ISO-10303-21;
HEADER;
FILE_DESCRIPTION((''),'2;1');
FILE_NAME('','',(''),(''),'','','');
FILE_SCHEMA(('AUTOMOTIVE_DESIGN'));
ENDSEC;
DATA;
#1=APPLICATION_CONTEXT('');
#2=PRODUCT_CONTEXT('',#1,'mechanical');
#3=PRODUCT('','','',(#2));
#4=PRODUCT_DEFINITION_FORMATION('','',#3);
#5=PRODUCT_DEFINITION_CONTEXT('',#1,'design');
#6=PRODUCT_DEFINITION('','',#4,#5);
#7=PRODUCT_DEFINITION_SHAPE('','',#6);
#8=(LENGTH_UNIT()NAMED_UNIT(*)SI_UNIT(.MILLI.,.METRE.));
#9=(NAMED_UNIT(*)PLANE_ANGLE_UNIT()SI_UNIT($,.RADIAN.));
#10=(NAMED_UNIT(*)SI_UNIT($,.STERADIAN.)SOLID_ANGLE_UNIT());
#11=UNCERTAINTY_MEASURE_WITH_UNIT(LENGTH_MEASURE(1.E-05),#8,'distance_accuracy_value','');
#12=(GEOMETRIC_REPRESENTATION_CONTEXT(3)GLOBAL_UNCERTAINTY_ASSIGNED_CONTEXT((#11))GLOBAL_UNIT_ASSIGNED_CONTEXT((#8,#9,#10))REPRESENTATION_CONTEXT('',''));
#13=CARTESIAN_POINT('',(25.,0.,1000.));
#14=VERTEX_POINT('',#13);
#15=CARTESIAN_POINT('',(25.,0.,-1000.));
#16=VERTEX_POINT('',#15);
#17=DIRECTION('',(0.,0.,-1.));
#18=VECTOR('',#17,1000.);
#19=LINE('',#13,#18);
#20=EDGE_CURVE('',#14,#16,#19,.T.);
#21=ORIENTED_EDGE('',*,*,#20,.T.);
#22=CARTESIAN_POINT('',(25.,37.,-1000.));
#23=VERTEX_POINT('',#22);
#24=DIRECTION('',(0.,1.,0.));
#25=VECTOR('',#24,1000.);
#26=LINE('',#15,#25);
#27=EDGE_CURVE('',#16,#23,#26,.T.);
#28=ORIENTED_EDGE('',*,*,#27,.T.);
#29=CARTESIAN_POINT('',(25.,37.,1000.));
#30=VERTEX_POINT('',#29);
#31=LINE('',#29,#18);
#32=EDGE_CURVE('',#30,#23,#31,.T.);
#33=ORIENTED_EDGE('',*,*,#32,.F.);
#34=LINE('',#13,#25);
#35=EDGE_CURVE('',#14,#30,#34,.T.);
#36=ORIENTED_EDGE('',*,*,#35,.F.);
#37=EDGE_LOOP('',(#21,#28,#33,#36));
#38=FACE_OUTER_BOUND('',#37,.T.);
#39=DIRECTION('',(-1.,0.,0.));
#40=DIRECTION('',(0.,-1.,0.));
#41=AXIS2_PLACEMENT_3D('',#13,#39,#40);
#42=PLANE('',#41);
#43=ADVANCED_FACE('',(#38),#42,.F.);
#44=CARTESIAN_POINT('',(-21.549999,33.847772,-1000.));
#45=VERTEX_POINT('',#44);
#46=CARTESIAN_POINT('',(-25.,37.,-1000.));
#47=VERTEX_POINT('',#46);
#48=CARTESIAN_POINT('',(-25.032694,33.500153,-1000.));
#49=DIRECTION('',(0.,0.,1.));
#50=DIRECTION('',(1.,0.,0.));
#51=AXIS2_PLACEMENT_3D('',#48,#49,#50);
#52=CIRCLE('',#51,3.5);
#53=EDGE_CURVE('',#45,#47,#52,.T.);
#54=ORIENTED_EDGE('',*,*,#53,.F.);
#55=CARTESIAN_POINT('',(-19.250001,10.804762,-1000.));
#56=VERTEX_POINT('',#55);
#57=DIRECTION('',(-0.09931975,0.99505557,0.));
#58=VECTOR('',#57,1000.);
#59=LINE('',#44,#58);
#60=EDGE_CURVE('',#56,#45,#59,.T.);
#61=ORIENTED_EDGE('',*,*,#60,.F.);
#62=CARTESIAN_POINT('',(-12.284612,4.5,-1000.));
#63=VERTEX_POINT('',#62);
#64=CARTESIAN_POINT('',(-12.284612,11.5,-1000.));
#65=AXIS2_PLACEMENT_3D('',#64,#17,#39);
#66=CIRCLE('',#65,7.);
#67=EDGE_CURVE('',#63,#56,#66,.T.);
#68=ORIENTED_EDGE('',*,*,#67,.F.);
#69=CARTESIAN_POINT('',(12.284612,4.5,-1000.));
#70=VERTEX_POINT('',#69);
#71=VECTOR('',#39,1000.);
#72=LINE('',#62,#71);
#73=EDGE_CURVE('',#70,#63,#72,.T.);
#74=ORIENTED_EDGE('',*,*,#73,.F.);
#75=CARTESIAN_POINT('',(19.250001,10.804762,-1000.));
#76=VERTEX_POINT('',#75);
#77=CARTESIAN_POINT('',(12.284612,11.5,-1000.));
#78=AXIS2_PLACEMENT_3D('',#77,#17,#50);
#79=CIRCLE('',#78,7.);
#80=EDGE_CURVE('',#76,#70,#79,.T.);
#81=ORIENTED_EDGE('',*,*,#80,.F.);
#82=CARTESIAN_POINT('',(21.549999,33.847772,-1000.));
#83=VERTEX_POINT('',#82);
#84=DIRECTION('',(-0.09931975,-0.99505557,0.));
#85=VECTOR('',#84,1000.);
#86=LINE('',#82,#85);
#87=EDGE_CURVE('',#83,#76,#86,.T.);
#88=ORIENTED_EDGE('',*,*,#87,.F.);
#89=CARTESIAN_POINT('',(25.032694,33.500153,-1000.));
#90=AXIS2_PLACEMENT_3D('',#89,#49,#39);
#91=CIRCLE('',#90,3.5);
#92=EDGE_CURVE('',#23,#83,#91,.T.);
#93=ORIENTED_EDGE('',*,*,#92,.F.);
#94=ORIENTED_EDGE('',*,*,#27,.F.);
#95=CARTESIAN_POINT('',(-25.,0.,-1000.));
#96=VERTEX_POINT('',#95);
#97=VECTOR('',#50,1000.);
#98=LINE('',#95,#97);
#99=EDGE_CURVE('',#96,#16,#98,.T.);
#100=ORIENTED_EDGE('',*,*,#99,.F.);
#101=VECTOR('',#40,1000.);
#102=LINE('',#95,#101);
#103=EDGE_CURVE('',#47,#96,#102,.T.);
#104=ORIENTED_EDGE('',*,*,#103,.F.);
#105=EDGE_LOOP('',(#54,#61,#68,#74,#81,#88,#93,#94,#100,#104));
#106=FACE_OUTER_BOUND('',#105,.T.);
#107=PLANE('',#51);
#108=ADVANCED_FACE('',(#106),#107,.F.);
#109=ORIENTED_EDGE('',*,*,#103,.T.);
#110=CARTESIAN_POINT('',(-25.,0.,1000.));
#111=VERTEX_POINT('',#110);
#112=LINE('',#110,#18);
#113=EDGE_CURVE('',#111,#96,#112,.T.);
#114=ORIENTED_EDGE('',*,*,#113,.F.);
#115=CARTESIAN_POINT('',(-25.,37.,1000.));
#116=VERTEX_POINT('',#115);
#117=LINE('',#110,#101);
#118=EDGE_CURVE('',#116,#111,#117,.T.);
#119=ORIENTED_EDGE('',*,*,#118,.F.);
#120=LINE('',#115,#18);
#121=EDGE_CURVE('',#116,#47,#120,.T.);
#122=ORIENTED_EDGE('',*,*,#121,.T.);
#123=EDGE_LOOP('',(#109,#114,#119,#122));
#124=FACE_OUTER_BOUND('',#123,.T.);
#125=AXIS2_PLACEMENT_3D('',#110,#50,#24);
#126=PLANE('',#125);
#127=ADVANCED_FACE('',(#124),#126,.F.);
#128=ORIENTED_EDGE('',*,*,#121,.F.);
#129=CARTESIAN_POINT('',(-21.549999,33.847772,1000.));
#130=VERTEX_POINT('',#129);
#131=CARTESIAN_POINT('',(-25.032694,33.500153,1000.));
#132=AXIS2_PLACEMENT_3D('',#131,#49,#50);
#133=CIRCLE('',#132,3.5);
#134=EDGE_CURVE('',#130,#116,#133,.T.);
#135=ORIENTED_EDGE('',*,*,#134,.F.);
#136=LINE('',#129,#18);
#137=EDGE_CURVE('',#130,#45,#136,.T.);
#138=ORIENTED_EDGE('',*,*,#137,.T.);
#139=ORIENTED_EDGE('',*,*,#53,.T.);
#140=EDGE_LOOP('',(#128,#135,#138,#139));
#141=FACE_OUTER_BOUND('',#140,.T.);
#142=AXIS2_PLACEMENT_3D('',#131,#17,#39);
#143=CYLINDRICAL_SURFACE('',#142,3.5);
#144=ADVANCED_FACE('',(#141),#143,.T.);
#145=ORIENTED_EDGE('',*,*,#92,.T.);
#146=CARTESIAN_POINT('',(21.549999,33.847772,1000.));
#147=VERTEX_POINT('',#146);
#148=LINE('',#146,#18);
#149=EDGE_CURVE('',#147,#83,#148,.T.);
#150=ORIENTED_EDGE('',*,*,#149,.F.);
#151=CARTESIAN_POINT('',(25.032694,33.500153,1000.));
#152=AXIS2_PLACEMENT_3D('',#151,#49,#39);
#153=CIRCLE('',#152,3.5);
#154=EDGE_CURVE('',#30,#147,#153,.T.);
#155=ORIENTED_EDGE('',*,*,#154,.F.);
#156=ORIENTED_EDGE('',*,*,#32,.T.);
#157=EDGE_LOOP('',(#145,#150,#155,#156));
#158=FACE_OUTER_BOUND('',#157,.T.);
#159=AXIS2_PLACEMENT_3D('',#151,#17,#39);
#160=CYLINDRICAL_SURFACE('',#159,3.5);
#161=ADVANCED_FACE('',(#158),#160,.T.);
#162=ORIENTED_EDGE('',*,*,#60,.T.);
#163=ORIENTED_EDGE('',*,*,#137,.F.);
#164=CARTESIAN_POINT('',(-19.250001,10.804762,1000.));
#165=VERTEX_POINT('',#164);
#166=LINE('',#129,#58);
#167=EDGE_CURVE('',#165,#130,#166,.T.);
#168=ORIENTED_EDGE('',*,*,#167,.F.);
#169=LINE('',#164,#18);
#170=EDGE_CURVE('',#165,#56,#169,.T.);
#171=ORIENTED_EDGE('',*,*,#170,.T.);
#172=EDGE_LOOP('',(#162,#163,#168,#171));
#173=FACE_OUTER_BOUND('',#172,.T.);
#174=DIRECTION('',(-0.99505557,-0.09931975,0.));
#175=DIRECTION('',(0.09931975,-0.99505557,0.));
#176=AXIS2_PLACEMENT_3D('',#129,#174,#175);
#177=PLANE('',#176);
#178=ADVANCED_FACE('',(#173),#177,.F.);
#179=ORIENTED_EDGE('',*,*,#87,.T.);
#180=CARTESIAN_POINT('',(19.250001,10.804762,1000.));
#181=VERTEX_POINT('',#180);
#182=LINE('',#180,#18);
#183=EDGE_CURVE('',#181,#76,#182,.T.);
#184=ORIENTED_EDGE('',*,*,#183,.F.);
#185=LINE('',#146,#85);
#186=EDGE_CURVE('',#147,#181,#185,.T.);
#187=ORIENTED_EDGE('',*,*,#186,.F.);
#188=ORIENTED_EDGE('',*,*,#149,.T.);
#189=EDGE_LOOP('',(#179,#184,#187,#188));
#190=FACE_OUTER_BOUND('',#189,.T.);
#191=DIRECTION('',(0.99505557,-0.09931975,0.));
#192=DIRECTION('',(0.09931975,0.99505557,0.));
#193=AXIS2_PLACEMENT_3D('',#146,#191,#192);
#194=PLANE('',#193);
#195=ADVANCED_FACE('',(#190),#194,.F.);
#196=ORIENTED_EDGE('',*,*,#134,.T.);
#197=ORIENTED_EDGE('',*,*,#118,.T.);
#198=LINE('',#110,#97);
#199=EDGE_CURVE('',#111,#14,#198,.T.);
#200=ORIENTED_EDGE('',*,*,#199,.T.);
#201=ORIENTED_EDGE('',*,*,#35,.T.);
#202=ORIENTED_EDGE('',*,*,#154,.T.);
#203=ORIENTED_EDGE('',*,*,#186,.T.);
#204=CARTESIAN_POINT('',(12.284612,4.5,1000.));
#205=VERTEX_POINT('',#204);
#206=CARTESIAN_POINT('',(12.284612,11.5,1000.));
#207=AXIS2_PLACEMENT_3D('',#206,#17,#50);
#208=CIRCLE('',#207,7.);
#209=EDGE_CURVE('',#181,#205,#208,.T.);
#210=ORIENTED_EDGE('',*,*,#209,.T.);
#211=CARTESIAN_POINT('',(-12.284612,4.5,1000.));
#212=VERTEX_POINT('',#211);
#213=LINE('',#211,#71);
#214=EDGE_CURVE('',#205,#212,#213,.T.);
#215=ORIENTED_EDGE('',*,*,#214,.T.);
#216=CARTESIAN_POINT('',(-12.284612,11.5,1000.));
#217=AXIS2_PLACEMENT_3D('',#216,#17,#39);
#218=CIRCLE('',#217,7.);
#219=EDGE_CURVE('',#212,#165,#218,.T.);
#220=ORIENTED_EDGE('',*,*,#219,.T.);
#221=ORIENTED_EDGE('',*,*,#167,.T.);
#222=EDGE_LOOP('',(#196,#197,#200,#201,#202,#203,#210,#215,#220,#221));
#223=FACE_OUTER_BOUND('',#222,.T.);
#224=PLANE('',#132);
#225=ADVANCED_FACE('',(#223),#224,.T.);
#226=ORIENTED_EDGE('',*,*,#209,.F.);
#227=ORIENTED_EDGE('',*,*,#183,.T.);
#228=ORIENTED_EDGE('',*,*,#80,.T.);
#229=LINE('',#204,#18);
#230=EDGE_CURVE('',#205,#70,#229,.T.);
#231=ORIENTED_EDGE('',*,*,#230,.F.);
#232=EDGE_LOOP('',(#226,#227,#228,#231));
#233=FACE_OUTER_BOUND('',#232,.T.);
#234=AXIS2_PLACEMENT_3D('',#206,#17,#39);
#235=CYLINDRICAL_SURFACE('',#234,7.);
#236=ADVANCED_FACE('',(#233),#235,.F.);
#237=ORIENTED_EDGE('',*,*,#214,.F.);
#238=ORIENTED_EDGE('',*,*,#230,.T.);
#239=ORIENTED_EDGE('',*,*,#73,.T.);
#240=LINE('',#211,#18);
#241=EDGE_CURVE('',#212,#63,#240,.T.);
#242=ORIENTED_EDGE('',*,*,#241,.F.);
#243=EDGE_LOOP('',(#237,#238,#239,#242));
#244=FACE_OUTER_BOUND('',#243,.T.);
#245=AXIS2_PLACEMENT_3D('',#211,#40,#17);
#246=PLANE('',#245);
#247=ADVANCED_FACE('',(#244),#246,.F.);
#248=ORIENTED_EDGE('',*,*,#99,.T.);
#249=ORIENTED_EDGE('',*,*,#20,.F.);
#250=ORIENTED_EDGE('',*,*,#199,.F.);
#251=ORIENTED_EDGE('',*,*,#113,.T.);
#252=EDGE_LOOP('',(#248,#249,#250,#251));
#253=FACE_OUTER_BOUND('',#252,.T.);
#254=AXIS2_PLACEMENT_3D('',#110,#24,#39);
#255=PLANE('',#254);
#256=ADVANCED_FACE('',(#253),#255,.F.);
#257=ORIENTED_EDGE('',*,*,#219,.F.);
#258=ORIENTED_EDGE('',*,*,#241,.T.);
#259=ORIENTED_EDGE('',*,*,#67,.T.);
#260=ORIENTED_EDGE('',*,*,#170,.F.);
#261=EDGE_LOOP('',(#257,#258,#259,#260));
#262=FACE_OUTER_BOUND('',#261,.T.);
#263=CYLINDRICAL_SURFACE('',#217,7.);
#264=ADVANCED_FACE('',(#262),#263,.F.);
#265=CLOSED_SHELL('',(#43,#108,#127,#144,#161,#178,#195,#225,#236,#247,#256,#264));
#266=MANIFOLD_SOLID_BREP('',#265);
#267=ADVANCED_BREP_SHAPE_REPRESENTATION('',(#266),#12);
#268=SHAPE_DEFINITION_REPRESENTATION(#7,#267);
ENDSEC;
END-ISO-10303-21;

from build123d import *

# Parameters (mm, degrees)
EXTRUDE1_DEPTH = 1000


with BuildPart() as part:
    # Sketch1 → Extrude1 (new, symmetric)
    with BuildSketch(Plane.XY):
        with BuildLine():
            Line((-25, 0), (25, 0))
            Line((25, 0), (25, 37))
            ThreePointArc((25, 37), (22.671841203, 36.084021126), (21.549999087, 33.847771823))
            Line((21.549999087, 33.847771823), (19.250000913, 10.804761752))
            ThreePointArc((19.250000913, 10.804761752), (16.982128941, 6.310266493), (12.284611923, 4.5))
            Line((12.284611923, 4.5), (-12.284611923, 4.5))
            ThreePointArc((-12.284611923, 4.5), (-16.982128941, 6.310266493), (-19.250000913, 10.804761752))
            Line((-19.250000913, 10.804761752), (-21.549999087, 33.847771823))
            ThreePointArc((-21.549999087, 33.847771823), (-22.671841203, 36.084021126), (-25, 37))
            Line((-25, 37), (-25, 0))
        make_face()
    extrude(amount=EXTRUDE1_DEPTH, both=True)


solid = part.part
